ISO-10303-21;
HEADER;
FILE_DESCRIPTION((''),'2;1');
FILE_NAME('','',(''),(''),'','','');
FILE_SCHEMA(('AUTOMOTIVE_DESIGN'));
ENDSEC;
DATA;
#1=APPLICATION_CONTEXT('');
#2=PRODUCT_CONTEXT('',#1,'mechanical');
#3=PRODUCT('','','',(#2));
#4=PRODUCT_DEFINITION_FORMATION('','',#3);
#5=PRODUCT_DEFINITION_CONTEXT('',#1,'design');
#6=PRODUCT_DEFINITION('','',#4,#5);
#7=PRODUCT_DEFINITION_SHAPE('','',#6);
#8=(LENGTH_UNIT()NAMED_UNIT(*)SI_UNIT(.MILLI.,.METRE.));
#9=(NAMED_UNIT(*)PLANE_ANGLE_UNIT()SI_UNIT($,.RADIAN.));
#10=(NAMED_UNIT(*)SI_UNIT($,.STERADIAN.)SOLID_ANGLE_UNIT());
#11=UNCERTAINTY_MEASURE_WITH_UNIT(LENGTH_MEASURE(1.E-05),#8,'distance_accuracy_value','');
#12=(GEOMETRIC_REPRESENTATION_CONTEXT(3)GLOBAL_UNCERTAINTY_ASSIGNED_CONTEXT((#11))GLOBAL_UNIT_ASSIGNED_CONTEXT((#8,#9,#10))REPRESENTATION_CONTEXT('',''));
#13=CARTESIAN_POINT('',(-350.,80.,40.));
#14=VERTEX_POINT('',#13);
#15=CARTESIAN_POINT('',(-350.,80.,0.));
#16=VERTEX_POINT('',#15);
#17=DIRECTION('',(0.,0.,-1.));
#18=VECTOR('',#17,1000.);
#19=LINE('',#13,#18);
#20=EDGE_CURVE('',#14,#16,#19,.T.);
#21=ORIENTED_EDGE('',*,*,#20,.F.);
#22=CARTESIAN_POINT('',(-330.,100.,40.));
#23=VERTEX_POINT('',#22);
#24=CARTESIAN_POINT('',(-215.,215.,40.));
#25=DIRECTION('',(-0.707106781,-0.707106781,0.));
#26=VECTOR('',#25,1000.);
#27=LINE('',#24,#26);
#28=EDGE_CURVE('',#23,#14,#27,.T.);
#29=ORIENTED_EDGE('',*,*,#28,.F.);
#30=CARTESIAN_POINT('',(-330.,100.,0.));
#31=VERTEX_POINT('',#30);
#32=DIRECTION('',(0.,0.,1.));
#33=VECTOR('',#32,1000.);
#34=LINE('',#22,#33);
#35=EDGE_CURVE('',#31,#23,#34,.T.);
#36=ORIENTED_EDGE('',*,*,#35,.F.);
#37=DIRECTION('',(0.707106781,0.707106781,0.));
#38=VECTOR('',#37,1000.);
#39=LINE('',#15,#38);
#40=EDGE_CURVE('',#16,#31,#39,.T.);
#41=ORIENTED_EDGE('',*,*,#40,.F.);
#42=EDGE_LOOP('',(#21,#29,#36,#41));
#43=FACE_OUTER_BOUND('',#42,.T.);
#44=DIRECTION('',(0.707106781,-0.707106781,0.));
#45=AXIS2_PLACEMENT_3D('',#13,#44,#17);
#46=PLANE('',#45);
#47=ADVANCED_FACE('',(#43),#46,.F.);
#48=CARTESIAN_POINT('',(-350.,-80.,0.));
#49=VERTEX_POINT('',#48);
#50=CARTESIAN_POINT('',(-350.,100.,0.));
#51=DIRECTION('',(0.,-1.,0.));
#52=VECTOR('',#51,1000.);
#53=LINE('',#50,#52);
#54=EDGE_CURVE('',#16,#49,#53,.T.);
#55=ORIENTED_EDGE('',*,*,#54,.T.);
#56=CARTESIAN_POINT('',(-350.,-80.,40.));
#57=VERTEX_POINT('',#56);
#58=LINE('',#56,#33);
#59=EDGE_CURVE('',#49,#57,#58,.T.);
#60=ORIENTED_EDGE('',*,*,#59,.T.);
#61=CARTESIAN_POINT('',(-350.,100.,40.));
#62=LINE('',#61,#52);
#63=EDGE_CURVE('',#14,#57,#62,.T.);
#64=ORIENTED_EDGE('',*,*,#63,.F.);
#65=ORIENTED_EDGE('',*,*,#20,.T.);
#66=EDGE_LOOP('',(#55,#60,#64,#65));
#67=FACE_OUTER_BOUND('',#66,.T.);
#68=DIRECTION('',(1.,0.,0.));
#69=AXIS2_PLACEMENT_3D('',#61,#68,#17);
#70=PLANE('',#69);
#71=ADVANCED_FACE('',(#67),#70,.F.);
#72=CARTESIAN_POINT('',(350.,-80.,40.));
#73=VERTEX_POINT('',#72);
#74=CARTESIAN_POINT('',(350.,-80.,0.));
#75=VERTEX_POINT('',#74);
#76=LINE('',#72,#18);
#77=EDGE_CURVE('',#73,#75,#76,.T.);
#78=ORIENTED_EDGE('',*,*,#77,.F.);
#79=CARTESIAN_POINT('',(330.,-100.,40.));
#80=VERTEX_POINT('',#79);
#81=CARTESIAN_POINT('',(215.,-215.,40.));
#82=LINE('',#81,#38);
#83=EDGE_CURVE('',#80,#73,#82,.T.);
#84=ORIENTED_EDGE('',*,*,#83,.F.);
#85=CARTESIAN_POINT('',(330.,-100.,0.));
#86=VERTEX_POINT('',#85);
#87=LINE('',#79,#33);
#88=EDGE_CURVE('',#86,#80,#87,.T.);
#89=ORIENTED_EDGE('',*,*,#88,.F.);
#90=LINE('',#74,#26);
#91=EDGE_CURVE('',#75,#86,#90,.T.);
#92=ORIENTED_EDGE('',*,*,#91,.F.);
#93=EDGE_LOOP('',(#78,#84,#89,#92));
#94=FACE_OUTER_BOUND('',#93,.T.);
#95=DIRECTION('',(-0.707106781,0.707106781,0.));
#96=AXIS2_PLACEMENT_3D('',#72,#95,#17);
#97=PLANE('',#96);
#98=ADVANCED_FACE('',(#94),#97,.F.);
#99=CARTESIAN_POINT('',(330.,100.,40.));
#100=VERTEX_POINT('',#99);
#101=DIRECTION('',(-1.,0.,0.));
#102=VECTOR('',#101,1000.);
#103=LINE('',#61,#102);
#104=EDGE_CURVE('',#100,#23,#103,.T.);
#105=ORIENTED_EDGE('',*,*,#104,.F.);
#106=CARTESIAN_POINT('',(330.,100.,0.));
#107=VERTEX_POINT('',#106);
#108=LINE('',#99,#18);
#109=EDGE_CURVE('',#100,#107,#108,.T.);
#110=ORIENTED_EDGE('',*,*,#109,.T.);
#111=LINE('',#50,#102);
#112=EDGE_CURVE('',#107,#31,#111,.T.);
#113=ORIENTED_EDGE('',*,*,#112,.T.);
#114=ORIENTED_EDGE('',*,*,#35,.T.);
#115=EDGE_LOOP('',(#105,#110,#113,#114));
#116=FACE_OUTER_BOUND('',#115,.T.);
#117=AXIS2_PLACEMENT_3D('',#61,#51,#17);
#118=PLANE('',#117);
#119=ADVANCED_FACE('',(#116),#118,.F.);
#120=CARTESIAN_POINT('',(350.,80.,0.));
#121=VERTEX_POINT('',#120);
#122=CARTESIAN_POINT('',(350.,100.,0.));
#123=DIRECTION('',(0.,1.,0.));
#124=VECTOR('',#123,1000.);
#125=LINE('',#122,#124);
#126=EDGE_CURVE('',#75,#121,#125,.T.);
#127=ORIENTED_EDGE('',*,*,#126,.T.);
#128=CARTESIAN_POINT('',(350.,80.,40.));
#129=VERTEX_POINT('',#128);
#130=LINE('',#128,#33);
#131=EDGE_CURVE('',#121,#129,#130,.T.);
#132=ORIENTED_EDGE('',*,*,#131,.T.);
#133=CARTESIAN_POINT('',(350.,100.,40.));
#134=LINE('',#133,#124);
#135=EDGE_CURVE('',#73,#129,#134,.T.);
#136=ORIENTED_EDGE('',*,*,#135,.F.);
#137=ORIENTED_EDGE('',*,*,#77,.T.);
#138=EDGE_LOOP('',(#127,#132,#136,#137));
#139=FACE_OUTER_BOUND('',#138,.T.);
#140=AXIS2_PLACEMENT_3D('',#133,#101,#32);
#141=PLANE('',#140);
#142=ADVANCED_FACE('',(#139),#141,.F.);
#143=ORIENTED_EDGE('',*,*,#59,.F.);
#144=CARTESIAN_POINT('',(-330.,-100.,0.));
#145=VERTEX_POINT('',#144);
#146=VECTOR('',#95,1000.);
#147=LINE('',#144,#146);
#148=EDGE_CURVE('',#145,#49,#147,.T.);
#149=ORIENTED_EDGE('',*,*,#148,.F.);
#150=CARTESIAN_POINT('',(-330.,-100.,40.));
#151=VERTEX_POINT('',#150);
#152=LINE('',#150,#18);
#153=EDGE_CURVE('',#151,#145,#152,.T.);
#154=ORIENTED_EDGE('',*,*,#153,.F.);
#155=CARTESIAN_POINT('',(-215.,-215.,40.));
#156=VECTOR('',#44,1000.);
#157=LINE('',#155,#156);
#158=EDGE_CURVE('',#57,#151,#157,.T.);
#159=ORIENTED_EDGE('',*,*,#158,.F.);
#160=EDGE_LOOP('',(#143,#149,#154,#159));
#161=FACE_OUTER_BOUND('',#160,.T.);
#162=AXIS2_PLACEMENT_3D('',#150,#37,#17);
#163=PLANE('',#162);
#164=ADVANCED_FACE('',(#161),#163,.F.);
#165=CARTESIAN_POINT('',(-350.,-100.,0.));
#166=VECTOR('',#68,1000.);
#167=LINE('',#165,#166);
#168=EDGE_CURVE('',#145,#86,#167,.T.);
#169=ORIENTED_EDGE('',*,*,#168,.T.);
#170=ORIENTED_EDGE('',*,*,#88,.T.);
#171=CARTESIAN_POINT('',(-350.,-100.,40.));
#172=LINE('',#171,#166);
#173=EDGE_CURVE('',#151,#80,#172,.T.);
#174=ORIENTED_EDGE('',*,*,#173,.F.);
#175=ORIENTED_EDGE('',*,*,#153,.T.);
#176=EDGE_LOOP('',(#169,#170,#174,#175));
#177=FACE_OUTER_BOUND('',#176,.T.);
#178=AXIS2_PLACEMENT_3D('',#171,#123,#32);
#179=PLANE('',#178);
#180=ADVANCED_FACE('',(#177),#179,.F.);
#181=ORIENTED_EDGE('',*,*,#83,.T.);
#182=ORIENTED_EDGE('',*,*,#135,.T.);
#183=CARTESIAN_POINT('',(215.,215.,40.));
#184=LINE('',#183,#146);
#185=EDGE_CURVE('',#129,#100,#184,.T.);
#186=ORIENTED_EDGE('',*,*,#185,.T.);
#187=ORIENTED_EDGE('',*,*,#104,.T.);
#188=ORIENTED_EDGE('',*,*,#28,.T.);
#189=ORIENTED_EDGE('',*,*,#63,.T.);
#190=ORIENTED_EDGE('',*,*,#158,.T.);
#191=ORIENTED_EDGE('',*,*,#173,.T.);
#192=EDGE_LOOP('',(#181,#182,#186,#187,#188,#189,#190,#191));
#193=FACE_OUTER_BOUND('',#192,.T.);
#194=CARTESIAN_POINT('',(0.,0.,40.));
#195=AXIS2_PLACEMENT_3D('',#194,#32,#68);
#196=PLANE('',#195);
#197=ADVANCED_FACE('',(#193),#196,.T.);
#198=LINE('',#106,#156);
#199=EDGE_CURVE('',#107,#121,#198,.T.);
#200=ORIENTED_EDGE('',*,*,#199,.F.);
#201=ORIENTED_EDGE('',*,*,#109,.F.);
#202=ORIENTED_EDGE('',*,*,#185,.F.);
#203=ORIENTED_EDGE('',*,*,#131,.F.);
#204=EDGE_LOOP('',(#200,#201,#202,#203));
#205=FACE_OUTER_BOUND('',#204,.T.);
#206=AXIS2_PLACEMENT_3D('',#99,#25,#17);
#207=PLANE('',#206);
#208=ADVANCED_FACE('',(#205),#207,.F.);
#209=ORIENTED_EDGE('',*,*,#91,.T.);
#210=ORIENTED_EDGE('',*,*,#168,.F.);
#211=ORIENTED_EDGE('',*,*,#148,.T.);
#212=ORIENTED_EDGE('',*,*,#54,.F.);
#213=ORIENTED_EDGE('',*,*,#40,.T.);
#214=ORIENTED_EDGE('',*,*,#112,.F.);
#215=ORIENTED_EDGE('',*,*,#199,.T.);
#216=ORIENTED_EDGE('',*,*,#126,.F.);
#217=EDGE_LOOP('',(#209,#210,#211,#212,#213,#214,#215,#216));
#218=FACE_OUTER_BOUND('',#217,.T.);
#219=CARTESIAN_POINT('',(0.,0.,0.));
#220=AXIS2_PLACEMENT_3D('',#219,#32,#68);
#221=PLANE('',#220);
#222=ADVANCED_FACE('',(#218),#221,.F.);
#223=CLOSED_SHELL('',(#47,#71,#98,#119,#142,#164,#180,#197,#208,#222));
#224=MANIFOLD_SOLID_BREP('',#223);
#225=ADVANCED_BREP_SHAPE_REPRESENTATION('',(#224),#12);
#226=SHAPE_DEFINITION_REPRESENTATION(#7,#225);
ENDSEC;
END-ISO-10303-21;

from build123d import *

# Parameters (mm, degrees)
SKETCH_1_W      = 700
SKETCH_1_H      = 200
EXTRUDE_1_DEPTH = 40
CHAMFER_1_SIZE  = 20


with BuildPart() as part:
    # 草图1 → 凸台-拉伸1 (new body)
    with BuildSketch(Plane.XY):
        Rectangle(SKETCH_1_W, SKETCH_1_H)
    extrude(amount=EXTRUDE_1_DEPTH)

    # 倒角1
    chamfer_1_edges = [part.edges().sort_by_distance(p)[0] for p in [
        (350, -100, 20),
        (-350, -100, 20),
        (-350, 100, 20),
        (350, 100, 20),
    ]]
    chamfer(chamfer_1_edges, length=CHAMFER_1_SIZE)


solid = part.part
